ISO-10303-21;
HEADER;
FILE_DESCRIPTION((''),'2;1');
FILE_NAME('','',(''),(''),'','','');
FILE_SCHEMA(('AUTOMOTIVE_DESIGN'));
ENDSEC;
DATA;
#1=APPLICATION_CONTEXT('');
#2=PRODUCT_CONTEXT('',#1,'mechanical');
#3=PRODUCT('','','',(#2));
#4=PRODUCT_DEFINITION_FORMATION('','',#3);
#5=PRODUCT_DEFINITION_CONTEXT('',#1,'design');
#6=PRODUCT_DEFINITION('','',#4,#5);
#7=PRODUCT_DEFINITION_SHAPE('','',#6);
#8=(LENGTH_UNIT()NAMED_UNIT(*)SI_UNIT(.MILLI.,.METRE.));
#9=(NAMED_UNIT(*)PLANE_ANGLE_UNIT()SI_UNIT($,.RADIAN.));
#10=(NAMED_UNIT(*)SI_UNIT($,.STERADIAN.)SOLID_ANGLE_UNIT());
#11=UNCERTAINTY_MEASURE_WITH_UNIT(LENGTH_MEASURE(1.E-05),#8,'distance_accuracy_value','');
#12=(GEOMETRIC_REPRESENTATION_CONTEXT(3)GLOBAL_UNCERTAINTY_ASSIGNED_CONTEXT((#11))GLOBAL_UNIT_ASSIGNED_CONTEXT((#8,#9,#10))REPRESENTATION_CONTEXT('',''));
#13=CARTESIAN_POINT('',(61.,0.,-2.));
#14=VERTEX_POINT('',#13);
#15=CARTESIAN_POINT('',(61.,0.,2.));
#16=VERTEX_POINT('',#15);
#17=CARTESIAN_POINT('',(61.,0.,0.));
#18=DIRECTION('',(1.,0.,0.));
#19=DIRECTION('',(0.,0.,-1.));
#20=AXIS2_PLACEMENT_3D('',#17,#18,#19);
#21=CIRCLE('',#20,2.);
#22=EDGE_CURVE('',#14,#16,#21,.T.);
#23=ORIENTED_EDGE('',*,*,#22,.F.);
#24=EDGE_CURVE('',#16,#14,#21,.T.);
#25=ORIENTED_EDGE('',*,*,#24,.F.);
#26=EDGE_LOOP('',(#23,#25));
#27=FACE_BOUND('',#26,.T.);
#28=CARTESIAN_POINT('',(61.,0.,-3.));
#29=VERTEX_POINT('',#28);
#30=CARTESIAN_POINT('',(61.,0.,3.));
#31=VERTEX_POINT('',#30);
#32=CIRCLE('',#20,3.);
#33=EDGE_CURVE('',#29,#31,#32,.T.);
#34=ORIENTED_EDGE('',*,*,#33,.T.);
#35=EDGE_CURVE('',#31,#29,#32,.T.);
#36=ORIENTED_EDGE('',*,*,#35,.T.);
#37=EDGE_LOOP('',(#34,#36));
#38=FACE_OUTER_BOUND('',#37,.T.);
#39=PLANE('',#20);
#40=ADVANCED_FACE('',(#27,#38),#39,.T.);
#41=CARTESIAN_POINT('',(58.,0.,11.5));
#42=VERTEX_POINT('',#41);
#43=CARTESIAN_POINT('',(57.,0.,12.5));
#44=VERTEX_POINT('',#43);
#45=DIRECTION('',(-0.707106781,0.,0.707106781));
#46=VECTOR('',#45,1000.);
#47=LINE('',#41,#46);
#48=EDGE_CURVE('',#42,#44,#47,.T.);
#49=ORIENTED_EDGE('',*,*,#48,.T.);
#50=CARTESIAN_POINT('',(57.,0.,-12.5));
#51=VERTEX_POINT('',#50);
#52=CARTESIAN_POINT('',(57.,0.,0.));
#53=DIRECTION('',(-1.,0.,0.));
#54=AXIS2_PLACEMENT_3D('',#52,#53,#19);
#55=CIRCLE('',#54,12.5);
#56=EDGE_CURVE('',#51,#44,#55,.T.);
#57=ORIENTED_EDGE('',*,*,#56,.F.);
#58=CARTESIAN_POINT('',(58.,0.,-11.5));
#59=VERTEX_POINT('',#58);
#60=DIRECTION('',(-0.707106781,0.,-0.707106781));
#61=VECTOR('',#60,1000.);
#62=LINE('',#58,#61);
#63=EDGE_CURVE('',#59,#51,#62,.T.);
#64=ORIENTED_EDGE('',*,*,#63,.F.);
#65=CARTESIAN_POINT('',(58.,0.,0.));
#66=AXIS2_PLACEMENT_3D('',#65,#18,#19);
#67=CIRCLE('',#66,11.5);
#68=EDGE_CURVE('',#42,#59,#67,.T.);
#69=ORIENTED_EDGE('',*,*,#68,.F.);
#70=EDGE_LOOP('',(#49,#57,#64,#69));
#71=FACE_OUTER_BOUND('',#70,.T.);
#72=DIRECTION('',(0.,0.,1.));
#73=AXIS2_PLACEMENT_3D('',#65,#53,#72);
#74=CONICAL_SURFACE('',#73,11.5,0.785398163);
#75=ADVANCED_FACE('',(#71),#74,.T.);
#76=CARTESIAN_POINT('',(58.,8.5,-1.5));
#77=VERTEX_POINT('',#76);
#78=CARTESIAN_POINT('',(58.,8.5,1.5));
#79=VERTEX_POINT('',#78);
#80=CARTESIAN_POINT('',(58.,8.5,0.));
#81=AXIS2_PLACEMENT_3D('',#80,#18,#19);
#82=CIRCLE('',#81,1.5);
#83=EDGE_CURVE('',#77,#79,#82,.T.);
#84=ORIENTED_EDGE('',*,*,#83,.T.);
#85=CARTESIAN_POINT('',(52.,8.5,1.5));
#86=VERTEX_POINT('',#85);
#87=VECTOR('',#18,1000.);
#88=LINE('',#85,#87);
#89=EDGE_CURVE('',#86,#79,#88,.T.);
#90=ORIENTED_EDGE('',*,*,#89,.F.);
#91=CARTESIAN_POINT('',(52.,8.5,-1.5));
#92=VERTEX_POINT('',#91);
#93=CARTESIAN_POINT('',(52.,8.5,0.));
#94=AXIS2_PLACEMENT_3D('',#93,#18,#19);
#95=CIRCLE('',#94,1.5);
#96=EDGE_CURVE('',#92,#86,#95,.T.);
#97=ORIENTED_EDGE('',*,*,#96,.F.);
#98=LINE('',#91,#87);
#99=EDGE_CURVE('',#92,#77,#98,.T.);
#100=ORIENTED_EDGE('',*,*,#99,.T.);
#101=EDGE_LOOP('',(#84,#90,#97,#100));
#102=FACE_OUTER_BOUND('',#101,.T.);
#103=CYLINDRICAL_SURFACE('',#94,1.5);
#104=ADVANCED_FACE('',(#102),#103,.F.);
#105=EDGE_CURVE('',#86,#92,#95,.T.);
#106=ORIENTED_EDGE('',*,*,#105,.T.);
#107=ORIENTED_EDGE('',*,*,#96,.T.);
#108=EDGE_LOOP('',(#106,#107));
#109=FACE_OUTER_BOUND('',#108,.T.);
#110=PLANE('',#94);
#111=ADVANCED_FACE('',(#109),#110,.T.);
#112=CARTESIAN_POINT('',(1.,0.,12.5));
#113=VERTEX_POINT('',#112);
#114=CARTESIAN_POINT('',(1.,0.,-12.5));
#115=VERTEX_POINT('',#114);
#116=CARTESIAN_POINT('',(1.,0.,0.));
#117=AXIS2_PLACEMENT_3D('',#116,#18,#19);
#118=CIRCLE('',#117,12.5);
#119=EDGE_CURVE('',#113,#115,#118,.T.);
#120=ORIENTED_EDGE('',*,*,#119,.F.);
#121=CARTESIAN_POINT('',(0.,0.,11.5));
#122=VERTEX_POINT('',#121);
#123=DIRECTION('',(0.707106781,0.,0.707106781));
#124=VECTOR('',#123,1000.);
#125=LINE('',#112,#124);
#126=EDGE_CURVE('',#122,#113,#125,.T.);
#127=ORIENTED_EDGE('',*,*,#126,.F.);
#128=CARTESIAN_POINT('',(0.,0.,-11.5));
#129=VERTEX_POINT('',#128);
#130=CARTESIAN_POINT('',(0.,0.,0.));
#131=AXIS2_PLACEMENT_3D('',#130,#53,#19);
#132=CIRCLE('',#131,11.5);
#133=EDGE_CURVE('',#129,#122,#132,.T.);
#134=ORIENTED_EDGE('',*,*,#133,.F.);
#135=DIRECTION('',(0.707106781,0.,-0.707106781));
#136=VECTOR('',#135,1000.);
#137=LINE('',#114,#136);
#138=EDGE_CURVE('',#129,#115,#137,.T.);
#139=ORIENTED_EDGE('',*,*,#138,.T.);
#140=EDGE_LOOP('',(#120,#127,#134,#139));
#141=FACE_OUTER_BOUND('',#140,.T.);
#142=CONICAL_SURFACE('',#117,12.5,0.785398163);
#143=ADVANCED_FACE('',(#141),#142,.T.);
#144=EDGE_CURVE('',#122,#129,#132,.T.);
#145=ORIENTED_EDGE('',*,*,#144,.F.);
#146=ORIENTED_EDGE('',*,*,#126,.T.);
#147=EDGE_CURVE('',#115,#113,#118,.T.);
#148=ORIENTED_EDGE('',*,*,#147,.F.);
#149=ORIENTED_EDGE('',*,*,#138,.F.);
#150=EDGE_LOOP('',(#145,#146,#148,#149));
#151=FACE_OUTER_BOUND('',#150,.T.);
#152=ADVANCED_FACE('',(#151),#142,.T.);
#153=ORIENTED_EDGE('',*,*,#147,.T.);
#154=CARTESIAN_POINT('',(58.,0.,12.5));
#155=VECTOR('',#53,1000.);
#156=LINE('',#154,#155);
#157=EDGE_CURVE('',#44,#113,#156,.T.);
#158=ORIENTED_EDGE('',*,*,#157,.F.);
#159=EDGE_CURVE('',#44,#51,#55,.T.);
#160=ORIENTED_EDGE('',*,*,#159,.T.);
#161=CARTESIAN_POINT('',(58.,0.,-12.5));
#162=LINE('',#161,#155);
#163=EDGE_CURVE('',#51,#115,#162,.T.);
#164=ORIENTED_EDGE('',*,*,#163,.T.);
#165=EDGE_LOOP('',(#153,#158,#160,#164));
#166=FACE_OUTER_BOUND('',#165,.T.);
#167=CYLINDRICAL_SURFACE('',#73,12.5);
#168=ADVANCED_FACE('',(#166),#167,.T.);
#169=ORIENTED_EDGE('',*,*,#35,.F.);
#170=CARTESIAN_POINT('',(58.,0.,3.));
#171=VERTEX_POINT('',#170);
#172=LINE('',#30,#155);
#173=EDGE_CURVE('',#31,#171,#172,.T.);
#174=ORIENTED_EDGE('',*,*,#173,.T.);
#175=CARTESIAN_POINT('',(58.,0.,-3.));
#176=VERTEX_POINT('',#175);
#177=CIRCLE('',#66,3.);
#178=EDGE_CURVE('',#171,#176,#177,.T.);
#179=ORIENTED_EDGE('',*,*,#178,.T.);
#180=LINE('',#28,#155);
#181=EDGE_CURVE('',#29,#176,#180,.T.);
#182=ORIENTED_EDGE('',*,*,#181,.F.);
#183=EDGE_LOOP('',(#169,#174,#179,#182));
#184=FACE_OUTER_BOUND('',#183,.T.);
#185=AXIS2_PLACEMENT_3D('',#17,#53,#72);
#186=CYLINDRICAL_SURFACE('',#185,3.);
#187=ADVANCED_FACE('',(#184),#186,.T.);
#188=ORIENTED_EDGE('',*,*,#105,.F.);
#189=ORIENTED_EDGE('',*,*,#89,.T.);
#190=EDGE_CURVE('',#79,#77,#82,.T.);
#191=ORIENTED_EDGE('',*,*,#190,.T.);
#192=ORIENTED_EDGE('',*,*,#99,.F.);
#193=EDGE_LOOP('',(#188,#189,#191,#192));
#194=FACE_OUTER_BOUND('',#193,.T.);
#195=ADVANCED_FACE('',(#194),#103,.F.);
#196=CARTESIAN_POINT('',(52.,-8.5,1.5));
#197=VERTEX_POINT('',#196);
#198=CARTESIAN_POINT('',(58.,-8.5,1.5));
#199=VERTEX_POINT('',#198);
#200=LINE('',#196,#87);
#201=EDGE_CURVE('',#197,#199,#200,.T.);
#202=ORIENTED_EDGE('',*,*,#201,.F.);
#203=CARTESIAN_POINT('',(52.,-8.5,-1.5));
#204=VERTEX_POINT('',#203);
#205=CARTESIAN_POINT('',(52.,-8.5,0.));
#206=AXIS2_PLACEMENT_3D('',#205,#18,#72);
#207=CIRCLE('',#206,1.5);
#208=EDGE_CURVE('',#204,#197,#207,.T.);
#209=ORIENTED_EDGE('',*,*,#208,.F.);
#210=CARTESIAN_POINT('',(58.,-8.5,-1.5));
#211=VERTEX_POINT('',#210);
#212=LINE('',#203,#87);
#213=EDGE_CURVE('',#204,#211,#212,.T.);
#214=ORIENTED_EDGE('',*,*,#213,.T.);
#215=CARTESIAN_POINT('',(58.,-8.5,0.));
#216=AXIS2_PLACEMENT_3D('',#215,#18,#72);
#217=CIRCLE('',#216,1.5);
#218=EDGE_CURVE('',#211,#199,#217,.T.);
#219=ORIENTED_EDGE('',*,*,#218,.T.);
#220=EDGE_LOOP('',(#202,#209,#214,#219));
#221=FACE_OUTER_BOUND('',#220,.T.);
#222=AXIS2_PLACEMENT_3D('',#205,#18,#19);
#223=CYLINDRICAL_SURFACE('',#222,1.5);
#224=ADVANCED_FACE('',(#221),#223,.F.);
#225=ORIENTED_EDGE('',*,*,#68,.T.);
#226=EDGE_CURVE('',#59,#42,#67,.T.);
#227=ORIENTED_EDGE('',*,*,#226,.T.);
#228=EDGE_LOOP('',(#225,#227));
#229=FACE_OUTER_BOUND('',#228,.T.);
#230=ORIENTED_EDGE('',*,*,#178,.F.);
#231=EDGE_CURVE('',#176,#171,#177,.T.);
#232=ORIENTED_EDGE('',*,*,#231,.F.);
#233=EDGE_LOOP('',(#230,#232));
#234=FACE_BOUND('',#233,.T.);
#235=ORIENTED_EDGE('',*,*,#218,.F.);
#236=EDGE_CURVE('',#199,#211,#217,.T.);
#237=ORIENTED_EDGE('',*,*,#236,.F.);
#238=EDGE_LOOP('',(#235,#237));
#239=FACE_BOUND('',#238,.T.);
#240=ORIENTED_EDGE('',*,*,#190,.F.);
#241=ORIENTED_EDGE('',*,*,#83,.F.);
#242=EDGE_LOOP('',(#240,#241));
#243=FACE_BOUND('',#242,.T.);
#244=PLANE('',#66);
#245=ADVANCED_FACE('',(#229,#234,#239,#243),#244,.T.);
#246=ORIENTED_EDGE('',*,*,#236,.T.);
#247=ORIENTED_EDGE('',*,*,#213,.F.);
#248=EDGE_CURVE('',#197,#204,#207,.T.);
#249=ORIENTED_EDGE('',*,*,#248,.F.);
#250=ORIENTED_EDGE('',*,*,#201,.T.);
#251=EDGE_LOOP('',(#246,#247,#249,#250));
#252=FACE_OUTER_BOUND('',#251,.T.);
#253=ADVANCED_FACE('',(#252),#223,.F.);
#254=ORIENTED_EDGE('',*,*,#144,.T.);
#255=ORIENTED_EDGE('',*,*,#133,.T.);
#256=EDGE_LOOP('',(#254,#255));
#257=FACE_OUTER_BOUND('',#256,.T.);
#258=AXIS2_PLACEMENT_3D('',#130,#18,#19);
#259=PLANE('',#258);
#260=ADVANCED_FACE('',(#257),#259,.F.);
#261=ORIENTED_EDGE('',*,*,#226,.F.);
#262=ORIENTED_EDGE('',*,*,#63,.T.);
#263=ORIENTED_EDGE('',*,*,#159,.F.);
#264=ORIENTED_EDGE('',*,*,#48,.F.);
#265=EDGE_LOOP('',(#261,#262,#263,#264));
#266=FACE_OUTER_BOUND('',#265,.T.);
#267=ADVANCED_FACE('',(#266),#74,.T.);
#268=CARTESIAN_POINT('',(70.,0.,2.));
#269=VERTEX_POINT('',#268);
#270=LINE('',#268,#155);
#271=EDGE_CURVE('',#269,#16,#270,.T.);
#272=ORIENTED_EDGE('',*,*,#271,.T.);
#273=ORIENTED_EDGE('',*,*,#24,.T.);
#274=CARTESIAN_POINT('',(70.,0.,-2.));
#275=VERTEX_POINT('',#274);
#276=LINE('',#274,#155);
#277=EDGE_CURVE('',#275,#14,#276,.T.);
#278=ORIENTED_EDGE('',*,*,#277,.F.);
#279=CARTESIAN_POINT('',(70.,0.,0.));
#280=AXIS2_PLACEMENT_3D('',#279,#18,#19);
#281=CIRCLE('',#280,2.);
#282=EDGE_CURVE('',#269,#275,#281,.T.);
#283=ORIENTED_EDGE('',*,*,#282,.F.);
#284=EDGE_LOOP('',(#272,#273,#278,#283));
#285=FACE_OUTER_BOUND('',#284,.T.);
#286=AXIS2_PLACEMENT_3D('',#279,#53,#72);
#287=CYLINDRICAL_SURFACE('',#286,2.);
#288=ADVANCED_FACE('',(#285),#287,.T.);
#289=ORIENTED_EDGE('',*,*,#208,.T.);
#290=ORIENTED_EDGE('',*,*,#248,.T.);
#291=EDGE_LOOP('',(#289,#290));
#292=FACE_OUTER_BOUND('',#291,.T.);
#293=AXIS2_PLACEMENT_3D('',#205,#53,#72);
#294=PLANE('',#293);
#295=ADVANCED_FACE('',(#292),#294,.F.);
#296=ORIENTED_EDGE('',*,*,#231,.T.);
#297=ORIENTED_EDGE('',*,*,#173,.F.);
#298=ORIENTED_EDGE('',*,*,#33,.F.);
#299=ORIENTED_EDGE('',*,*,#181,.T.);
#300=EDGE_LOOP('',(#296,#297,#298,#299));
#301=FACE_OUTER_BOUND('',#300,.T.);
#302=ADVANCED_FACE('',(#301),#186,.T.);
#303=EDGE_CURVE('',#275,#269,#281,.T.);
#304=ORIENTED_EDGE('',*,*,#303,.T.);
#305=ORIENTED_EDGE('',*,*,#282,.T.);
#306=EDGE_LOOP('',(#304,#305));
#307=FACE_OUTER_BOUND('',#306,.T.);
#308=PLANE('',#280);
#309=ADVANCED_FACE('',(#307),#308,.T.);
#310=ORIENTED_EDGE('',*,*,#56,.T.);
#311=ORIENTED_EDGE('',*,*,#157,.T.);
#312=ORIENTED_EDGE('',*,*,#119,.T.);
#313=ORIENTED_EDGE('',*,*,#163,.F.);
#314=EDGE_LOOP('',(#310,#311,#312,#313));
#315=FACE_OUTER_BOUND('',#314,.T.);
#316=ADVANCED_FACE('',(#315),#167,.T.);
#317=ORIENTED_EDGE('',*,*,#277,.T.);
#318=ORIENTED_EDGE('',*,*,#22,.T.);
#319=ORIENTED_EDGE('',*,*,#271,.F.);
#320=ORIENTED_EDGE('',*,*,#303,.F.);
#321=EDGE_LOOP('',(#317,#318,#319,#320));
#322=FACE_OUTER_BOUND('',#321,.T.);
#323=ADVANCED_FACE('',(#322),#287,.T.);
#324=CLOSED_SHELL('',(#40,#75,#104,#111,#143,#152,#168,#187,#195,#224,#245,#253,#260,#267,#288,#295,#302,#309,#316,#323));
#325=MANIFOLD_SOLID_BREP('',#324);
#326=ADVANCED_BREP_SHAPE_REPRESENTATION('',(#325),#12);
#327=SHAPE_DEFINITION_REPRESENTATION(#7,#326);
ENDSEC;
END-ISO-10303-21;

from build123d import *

# Parameters (mm, degrees)
SKETCH1_R           = 12.5
BOSS_EXTRUDE1_DEPTH = 58
SKETCH2_R           = 3
BOSS_EXTRUDE2_DEPTH = 3
SKETCH3_R           = 2
BOSS_EXTRUDE3_DEPTH = 9
SKETCH4_R           = 1.5
CUT_EXTRUDE1_DEPTH  = 6
CHAMFER1_SIZE       = 1
CHAMFER2_SIZE       = 1


with BuildPart() as part:
    # Sketch1 → Boss-Extrude1 (new body)
    with BuildSketch(Plane(origin=(0, 0, 0), x_dir=(0, 0, -1), z_dir=(1, 0, 0))):
        with Locations(Location((0, 0, 0), (0, 0, 180))):
            Circle(SKETCH1_R)
    extrude(amount=BOSS_EXTRUDE1_DEPTH)

    # Sketch2 → Boss-Extrude2 (add)
    with BuildSketch(Plane(origin=(58, 0, 0), x_dir=(0, 0, -1), z_dir=(1, 0, 0))):
        Circle(SKETCH2_R)
    extrude(amount=BOSS_EXTRUDE2_DEPTH)

    # Sketch3 → Boss-Extrude3 (add)
    with BuildSketch(Plane(origin=(61, 0, 0), x_dir=(0, 0, -1), z_dir=(1, 0, 0))):
        Circle(SKETCH3_R)
    extrude(amount=BOSS_EXTRUDE3_DEPTH)

    # Sketch4 → Cut-Extrude1 (cut)
    with BuildSketch(Plane(origin=(58, 0, 0), x_dir=(0, 0, -1), z_dir=(1, 0, 0))):
        with Locations((0, 8.5)):
            Circle(SKETCH4_R)
        with Locations(Location((0, -8.5, 0), (0, 0, 180))):
            Circle(SKETCH4_R)
    extrude(amount=-CUT_EXTRUDE1_DEPTH, mode=Mode.SUBTRACT)

    # Chamfer1
    chamfer1_edges = [part.edges().sort_by_distance(p)[0] for p in [
        (58, 0, -12.5),
    ]]
    chamfer(chamfer1_edges, length=CHAMFER1_SIZE)

    # Chamfer2
    chamfer2_edges = [part.edges().sort_by_distance(p)[0] for p in [
        (0, 0, -12.5),
    ]]
    chamfer(chamfer2_edges, length=CHAMFER2_SIZE)


solid = part.part
